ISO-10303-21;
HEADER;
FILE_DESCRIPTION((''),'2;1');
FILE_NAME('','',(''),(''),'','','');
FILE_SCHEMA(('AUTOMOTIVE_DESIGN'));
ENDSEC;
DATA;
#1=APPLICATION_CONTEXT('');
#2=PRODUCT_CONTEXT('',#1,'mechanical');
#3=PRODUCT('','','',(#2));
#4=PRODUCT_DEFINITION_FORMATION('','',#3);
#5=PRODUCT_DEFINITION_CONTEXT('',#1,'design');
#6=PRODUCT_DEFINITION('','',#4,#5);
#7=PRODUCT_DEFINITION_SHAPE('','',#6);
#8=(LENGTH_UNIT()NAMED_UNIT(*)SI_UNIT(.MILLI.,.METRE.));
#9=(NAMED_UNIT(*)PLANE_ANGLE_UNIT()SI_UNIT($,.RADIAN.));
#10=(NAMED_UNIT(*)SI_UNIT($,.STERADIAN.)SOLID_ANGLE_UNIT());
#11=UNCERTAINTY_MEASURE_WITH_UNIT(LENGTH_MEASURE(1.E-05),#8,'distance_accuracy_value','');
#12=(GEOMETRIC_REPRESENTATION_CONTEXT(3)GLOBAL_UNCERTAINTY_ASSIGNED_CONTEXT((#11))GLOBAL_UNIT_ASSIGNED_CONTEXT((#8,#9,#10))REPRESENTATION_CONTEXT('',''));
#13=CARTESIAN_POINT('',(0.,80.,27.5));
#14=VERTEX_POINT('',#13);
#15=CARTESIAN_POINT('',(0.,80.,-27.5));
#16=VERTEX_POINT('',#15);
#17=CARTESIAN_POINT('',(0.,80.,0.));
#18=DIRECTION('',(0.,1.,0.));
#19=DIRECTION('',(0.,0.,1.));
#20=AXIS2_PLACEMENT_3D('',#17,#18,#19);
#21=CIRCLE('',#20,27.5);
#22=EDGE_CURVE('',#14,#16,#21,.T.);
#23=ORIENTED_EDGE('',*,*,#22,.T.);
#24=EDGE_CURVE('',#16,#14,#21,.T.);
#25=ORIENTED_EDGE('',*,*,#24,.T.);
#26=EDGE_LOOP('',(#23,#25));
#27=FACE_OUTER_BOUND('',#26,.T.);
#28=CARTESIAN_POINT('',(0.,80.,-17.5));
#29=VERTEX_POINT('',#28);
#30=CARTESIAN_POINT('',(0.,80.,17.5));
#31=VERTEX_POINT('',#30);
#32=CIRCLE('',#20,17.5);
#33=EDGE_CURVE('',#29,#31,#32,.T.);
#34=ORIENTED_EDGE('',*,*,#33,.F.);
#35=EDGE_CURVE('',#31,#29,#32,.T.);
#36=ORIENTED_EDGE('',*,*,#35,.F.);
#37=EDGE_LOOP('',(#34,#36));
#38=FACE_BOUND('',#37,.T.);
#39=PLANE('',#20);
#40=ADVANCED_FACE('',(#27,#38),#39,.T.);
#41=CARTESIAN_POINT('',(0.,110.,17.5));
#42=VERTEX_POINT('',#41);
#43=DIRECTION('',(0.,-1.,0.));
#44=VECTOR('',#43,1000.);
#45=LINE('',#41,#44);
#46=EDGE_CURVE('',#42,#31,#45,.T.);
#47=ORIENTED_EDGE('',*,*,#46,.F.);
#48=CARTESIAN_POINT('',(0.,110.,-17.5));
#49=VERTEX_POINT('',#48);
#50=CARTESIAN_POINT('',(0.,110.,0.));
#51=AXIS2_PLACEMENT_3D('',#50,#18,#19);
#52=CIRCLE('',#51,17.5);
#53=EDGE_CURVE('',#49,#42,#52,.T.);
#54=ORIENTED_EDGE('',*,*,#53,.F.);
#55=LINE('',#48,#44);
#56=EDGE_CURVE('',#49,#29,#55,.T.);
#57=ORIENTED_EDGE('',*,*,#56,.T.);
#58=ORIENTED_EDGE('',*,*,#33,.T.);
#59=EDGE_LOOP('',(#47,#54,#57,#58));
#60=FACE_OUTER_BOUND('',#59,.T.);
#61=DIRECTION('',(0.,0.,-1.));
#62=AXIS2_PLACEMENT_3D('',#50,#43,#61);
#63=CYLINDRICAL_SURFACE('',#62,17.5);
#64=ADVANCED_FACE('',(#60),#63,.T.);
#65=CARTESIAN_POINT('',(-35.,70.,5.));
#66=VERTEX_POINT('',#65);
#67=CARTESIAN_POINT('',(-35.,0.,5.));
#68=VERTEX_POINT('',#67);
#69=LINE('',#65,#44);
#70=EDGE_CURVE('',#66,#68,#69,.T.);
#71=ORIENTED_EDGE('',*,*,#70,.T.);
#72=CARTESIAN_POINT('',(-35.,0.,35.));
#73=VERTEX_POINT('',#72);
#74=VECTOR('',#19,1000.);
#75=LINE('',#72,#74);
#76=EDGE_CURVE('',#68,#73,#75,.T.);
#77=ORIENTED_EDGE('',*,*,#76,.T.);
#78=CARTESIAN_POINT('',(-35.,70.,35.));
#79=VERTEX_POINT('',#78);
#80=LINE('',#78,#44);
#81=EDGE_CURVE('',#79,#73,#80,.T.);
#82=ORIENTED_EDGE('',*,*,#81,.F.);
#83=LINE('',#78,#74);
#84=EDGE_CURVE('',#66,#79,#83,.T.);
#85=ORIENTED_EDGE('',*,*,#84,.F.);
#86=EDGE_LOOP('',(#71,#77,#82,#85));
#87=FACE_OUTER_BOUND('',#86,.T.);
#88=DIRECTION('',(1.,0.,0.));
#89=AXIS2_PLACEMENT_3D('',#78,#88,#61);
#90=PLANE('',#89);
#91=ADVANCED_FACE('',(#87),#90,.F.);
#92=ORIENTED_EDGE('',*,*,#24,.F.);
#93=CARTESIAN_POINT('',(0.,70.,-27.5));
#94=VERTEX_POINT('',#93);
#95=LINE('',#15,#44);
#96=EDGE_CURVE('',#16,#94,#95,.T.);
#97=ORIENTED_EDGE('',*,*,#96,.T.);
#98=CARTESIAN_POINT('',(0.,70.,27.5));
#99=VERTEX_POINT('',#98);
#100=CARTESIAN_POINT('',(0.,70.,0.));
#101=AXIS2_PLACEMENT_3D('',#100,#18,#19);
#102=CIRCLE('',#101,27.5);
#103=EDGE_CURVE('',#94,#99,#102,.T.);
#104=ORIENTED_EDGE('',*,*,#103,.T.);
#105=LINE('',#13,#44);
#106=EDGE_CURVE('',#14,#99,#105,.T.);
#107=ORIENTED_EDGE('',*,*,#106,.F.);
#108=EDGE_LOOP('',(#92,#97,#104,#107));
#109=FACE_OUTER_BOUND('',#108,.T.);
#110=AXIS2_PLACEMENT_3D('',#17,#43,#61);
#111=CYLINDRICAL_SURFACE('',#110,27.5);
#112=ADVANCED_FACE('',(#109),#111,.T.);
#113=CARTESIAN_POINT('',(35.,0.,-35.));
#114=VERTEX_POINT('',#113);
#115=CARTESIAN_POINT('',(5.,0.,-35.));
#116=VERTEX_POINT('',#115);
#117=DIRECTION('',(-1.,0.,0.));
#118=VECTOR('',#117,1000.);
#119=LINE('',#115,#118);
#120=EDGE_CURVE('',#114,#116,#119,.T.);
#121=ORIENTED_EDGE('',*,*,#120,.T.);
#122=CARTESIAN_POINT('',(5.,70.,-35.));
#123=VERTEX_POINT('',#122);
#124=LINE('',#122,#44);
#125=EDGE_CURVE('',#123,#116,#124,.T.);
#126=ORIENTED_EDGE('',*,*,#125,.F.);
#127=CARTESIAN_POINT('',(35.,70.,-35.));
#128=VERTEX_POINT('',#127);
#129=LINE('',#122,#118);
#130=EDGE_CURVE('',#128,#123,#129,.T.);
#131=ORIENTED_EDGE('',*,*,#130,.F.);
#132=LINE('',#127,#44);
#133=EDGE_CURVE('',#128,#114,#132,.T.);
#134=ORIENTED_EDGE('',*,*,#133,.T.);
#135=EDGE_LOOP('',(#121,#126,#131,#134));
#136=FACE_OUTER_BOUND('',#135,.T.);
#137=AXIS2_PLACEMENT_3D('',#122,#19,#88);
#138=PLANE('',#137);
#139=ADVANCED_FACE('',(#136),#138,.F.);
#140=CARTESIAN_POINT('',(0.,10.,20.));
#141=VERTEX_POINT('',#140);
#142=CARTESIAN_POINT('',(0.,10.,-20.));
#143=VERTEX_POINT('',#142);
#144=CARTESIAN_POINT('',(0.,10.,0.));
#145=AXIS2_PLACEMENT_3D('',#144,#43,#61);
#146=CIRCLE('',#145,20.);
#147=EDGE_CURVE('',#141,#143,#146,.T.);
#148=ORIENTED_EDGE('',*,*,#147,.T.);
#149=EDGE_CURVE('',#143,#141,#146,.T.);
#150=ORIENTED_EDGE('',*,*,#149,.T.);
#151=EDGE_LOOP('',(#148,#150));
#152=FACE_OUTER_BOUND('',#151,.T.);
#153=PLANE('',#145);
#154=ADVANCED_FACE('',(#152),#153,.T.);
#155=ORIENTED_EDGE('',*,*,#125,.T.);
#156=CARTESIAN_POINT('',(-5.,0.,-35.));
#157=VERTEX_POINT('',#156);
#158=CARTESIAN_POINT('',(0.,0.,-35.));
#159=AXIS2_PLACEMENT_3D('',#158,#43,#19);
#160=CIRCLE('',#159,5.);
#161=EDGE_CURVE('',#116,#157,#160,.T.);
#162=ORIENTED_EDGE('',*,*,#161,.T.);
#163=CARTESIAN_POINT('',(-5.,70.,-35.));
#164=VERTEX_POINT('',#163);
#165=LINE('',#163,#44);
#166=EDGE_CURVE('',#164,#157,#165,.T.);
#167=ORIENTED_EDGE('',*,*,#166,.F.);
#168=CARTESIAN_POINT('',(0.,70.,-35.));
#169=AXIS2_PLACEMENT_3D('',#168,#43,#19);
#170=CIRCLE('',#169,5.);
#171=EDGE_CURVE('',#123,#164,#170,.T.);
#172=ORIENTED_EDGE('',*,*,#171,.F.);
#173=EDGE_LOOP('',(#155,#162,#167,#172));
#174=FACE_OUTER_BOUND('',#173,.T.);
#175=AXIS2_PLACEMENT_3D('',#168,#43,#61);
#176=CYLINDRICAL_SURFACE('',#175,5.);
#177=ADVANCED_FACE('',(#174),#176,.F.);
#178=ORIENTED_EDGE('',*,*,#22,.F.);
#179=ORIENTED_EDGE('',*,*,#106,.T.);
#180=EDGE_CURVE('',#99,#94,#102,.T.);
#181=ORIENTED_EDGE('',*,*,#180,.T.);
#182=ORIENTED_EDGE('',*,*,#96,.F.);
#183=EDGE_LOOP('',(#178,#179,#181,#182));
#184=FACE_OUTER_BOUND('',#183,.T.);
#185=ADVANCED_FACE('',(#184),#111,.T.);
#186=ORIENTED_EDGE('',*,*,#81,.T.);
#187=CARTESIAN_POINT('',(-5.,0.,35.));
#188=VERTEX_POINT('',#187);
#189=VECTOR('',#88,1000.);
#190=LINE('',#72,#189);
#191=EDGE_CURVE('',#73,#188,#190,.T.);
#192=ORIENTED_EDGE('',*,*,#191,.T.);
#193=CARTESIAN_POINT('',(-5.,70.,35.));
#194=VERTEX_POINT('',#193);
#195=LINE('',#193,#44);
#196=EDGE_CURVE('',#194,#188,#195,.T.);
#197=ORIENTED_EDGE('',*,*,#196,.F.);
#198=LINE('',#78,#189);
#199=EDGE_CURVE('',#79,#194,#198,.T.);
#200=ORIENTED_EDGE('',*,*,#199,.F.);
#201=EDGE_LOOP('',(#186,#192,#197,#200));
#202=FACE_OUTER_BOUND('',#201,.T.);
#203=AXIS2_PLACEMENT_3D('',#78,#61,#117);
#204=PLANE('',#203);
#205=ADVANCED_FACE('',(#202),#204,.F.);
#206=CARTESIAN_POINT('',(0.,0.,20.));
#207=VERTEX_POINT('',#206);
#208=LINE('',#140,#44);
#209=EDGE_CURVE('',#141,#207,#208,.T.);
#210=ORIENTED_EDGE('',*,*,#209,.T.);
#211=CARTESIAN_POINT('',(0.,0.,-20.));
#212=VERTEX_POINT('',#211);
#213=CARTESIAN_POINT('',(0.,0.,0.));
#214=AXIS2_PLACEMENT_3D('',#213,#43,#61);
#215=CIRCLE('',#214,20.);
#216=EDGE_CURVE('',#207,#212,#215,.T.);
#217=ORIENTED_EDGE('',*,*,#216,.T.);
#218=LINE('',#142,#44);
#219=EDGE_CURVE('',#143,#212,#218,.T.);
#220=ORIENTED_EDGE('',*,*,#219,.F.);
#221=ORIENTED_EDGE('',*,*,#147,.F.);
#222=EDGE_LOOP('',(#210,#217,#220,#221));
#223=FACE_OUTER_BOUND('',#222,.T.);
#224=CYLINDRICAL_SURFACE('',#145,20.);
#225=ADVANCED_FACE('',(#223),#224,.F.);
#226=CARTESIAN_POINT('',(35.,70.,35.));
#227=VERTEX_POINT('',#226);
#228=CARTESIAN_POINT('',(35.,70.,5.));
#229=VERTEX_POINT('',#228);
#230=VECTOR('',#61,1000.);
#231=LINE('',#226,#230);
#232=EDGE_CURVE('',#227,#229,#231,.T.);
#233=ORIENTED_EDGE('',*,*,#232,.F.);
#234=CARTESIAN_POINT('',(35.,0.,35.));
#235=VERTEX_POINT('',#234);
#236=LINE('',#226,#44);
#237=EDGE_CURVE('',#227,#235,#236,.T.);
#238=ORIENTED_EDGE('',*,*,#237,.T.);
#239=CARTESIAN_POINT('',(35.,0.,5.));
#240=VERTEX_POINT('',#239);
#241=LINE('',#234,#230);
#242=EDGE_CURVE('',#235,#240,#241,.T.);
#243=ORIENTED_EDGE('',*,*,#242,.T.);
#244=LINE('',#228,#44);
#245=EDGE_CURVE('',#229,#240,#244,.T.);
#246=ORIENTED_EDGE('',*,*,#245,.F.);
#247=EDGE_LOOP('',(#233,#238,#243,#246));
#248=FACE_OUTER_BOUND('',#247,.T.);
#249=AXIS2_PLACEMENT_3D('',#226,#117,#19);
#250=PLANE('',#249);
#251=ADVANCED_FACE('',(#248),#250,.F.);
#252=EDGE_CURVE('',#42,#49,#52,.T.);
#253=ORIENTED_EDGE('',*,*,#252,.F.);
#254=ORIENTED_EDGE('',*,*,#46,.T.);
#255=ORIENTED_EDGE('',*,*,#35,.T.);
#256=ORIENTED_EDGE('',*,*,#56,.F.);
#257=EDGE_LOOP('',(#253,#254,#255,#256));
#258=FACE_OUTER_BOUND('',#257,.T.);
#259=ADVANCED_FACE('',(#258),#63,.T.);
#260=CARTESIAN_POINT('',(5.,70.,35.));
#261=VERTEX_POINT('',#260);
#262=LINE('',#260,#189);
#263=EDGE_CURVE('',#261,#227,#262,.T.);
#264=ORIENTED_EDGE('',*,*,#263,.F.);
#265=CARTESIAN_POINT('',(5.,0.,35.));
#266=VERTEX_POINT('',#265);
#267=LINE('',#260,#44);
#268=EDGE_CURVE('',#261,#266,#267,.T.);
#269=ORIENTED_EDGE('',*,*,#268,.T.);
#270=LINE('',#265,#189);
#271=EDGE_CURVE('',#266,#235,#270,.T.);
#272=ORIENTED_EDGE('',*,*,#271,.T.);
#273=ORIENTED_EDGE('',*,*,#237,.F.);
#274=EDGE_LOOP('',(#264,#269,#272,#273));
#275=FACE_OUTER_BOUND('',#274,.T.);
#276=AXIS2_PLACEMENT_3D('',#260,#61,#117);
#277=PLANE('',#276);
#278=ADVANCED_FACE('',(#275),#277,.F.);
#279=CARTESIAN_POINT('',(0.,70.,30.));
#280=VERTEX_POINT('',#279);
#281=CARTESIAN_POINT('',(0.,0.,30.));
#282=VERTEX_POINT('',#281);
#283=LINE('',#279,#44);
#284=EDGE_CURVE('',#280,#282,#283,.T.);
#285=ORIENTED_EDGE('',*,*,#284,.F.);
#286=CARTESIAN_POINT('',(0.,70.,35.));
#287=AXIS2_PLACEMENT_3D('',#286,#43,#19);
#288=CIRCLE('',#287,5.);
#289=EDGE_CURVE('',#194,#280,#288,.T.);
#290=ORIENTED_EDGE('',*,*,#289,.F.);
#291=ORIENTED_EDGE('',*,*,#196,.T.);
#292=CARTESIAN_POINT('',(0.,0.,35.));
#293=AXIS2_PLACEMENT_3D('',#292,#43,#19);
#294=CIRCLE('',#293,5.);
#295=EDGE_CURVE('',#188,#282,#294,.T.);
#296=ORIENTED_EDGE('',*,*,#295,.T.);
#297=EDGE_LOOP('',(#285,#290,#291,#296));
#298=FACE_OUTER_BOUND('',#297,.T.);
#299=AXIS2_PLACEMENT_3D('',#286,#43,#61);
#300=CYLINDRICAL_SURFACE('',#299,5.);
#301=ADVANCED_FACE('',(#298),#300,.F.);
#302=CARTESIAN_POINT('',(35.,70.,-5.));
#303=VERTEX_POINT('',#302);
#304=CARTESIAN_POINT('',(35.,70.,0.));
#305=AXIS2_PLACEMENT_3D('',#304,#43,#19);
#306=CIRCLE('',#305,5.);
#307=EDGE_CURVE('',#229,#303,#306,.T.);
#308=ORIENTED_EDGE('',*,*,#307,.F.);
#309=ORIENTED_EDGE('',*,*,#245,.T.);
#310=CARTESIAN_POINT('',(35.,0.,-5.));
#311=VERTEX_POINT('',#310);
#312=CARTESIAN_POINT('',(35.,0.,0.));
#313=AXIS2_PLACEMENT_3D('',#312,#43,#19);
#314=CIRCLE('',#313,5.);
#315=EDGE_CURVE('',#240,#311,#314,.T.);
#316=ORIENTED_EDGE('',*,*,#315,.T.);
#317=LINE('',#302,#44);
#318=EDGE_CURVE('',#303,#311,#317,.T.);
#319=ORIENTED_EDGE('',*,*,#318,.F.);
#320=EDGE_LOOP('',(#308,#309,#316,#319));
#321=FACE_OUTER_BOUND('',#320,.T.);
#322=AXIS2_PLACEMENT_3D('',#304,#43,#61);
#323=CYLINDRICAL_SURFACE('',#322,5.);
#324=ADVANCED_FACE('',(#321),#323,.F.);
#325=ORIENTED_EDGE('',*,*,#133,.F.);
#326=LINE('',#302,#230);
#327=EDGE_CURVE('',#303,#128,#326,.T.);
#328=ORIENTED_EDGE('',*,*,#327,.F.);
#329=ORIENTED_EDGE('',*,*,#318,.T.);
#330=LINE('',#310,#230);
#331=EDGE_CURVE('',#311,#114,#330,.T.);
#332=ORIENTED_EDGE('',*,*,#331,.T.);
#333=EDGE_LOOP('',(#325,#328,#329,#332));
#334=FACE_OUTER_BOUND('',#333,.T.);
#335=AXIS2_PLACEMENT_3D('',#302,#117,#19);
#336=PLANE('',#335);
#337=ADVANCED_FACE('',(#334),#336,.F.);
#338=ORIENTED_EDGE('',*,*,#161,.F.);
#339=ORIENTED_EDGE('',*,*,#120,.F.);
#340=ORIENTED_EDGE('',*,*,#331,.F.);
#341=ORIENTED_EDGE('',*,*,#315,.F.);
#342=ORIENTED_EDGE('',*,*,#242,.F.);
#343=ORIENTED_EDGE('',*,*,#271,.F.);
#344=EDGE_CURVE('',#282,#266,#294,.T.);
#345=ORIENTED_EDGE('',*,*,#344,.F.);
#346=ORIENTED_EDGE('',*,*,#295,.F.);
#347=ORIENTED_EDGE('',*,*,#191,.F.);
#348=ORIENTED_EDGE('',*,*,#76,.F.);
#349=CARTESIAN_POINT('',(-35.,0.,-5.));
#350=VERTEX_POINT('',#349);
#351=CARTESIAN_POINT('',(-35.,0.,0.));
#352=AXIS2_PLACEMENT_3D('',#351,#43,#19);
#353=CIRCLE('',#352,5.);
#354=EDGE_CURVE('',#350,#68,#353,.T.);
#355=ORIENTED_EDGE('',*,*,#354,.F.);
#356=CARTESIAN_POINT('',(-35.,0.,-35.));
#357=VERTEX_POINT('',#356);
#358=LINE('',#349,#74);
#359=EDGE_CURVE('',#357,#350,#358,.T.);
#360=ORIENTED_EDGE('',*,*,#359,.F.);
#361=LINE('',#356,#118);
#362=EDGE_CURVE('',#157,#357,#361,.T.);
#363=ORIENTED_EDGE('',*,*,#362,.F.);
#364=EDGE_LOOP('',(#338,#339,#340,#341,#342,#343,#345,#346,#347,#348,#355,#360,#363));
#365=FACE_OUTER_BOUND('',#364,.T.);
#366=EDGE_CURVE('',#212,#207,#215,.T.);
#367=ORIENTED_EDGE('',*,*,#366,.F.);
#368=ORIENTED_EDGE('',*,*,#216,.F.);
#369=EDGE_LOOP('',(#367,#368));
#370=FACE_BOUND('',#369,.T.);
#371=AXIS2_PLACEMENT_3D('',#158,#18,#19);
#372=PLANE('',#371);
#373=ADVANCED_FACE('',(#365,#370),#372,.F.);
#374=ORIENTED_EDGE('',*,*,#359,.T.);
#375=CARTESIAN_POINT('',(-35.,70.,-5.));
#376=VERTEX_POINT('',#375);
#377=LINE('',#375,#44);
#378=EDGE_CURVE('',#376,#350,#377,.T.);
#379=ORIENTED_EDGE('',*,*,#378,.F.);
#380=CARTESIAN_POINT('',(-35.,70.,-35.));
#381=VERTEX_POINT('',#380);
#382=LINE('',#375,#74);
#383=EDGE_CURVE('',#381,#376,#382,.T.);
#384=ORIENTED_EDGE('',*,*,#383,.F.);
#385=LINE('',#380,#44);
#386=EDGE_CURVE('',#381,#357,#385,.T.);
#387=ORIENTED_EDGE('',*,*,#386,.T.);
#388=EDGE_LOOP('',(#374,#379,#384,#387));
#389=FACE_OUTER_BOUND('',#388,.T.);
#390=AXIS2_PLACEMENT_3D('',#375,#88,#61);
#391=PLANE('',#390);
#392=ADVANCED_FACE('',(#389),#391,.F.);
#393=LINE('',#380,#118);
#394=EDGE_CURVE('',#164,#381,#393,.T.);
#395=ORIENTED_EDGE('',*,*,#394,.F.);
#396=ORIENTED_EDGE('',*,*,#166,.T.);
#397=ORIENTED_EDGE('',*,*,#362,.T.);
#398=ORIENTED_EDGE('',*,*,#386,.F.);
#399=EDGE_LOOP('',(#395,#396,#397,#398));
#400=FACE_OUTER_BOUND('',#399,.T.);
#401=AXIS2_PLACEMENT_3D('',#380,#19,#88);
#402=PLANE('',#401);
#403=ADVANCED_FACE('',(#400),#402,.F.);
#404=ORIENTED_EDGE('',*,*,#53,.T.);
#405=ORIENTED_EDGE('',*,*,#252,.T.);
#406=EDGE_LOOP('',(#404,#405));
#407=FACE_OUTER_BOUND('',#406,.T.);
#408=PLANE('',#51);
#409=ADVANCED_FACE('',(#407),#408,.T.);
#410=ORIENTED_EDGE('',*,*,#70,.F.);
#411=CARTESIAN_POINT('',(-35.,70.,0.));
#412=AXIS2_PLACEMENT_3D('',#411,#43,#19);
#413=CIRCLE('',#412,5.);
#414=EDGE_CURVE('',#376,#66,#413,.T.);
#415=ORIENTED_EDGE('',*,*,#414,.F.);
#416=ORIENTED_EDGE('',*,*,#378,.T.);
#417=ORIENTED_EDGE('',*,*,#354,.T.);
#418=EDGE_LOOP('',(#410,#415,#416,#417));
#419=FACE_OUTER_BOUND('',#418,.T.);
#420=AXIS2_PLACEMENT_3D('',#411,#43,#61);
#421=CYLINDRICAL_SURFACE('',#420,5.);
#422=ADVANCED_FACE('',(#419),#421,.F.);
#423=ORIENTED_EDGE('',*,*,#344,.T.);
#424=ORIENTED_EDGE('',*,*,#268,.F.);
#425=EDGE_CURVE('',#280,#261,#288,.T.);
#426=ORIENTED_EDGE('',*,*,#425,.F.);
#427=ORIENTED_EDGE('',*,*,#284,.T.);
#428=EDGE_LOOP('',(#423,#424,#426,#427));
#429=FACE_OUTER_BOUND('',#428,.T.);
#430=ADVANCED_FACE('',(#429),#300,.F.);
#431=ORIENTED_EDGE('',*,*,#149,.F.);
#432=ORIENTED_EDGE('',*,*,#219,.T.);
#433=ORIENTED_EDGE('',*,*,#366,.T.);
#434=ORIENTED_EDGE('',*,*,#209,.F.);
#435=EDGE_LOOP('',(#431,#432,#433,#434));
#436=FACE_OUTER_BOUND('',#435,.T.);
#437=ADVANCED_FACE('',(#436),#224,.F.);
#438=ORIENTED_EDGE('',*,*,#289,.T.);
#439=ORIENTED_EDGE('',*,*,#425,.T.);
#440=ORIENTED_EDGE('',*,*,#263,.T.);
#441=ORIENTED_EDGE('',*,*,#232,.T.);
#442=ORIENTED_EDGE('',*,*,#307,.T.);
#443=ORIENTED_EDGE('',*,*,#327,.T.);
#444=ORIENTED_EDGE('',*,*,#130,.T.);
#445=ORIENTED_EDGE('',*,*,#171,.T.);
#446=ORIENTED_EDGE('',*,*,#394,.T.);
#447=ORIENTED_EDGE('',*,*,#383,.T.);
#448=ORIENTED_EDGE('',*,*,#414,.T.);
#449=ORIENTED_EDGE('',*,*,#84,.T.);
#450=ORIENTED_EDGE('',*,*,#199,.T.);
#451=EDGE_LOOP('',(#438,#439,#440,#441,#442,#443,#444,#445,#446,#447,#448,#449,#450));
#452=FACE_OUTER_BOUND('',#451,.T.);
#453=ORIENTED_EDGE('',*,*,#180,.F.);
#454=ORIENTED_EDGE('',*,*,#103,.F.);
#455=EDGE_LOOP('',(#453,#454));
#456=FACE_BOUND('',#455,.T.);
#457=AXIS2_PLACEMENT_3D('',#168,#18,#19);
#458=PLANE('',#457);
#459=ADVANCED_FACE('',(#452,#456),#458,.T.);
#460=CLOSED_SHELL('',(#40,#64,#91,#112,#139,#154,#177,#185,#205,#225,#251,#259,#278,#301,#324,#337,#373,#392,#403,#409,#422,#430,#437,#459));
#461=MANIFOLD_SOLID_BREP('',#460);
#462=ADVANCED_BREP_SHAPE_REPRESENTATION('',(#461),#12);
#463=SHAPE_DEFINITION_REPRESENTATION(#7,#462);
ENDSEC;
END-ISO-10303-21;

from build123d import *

# Parameters (mm, degrees)
BOSS_EXTRUDE1_DEPTH = 70
SKETCH2_R           = 20
CUT_EXTRUDE1_DEPTH  = 10
SKETCH3_R           = 27.5
BOSS_EXTRUDE2_DEPTH = 10
SKETCH4_R           = 17.5
BOSS_EXTRUDE3_DEPTH = 30


with BuildPart() as part:
    # Sketch1 → Boss-Extrude1 (new body)
    with BuildSketch(Plane(origin=(0, 0, 0), x_dir=(1, 0, 0), z_dir=(0, 1, 0))):
        with BuildLine():
            Line((5, 35), (35, 35))
            Line((35, 35), (35, 5))
            ThreePointArc((35, 5), (30, 0), (35, -5))
            Line((35, -5), (35, -35))
            Line((35, -35), (5, -35))
            ThreePointArc((5, -35), (0, -30), (-5, -35))
            Line((-5, -35), (-35, -35))
            Line((-35, -35), (-35, -5))
            ThreePointArc((-35, -5), (-30, 0), (-35, 5))
            Line((-35, 5), (-35, 35))
            Line((-35, 35), (-5, 35))
            ThreePointArc((-5, 35), (0, 30), (5, 35))
        make_face()
    extrude(amount=BOSS_EXTRUDE1_DEPTH)

    # Sketch2 → Cut-Extrude1 (cut)
    with BuildSketch(Plane.XZ):
        with Locations(Location((0, 0, 0), (0, 0, 270))):
            Circle(SKETCH2_R)
    extrude(amount=-CUT_EXTRUDE1_DEPTH, mode=Mode.SUBTRACT)

    # Sketch3 → Boss-Extrude2 (add)
    with BuildSketch(Plane(origin=(0, 70, 0), x_dir=(1, 0, 0), z_dir=(0, 1, 0))):
        with Locations(Location((0, 0, 0), (0, 0, 270))):
            Circle(SKETCH3_R)
    extrude(amount=BOSS_EXTRUDE2_DEPTH)

    # Sketch4 → Boss-Extrude3 (add)
    with BuildSketch(Plane(origin=(0, 80, 0), x_dir=(1, 0, 0), z_dir=(0, 1, 0))):
        with Locations(Location((0, 0, 0), (0, 0, 270))):
            Circle(SKETCH4_R)
    extrude(amount=BOSS_EXTRUDE3_DEPTH)


solid = part.part
